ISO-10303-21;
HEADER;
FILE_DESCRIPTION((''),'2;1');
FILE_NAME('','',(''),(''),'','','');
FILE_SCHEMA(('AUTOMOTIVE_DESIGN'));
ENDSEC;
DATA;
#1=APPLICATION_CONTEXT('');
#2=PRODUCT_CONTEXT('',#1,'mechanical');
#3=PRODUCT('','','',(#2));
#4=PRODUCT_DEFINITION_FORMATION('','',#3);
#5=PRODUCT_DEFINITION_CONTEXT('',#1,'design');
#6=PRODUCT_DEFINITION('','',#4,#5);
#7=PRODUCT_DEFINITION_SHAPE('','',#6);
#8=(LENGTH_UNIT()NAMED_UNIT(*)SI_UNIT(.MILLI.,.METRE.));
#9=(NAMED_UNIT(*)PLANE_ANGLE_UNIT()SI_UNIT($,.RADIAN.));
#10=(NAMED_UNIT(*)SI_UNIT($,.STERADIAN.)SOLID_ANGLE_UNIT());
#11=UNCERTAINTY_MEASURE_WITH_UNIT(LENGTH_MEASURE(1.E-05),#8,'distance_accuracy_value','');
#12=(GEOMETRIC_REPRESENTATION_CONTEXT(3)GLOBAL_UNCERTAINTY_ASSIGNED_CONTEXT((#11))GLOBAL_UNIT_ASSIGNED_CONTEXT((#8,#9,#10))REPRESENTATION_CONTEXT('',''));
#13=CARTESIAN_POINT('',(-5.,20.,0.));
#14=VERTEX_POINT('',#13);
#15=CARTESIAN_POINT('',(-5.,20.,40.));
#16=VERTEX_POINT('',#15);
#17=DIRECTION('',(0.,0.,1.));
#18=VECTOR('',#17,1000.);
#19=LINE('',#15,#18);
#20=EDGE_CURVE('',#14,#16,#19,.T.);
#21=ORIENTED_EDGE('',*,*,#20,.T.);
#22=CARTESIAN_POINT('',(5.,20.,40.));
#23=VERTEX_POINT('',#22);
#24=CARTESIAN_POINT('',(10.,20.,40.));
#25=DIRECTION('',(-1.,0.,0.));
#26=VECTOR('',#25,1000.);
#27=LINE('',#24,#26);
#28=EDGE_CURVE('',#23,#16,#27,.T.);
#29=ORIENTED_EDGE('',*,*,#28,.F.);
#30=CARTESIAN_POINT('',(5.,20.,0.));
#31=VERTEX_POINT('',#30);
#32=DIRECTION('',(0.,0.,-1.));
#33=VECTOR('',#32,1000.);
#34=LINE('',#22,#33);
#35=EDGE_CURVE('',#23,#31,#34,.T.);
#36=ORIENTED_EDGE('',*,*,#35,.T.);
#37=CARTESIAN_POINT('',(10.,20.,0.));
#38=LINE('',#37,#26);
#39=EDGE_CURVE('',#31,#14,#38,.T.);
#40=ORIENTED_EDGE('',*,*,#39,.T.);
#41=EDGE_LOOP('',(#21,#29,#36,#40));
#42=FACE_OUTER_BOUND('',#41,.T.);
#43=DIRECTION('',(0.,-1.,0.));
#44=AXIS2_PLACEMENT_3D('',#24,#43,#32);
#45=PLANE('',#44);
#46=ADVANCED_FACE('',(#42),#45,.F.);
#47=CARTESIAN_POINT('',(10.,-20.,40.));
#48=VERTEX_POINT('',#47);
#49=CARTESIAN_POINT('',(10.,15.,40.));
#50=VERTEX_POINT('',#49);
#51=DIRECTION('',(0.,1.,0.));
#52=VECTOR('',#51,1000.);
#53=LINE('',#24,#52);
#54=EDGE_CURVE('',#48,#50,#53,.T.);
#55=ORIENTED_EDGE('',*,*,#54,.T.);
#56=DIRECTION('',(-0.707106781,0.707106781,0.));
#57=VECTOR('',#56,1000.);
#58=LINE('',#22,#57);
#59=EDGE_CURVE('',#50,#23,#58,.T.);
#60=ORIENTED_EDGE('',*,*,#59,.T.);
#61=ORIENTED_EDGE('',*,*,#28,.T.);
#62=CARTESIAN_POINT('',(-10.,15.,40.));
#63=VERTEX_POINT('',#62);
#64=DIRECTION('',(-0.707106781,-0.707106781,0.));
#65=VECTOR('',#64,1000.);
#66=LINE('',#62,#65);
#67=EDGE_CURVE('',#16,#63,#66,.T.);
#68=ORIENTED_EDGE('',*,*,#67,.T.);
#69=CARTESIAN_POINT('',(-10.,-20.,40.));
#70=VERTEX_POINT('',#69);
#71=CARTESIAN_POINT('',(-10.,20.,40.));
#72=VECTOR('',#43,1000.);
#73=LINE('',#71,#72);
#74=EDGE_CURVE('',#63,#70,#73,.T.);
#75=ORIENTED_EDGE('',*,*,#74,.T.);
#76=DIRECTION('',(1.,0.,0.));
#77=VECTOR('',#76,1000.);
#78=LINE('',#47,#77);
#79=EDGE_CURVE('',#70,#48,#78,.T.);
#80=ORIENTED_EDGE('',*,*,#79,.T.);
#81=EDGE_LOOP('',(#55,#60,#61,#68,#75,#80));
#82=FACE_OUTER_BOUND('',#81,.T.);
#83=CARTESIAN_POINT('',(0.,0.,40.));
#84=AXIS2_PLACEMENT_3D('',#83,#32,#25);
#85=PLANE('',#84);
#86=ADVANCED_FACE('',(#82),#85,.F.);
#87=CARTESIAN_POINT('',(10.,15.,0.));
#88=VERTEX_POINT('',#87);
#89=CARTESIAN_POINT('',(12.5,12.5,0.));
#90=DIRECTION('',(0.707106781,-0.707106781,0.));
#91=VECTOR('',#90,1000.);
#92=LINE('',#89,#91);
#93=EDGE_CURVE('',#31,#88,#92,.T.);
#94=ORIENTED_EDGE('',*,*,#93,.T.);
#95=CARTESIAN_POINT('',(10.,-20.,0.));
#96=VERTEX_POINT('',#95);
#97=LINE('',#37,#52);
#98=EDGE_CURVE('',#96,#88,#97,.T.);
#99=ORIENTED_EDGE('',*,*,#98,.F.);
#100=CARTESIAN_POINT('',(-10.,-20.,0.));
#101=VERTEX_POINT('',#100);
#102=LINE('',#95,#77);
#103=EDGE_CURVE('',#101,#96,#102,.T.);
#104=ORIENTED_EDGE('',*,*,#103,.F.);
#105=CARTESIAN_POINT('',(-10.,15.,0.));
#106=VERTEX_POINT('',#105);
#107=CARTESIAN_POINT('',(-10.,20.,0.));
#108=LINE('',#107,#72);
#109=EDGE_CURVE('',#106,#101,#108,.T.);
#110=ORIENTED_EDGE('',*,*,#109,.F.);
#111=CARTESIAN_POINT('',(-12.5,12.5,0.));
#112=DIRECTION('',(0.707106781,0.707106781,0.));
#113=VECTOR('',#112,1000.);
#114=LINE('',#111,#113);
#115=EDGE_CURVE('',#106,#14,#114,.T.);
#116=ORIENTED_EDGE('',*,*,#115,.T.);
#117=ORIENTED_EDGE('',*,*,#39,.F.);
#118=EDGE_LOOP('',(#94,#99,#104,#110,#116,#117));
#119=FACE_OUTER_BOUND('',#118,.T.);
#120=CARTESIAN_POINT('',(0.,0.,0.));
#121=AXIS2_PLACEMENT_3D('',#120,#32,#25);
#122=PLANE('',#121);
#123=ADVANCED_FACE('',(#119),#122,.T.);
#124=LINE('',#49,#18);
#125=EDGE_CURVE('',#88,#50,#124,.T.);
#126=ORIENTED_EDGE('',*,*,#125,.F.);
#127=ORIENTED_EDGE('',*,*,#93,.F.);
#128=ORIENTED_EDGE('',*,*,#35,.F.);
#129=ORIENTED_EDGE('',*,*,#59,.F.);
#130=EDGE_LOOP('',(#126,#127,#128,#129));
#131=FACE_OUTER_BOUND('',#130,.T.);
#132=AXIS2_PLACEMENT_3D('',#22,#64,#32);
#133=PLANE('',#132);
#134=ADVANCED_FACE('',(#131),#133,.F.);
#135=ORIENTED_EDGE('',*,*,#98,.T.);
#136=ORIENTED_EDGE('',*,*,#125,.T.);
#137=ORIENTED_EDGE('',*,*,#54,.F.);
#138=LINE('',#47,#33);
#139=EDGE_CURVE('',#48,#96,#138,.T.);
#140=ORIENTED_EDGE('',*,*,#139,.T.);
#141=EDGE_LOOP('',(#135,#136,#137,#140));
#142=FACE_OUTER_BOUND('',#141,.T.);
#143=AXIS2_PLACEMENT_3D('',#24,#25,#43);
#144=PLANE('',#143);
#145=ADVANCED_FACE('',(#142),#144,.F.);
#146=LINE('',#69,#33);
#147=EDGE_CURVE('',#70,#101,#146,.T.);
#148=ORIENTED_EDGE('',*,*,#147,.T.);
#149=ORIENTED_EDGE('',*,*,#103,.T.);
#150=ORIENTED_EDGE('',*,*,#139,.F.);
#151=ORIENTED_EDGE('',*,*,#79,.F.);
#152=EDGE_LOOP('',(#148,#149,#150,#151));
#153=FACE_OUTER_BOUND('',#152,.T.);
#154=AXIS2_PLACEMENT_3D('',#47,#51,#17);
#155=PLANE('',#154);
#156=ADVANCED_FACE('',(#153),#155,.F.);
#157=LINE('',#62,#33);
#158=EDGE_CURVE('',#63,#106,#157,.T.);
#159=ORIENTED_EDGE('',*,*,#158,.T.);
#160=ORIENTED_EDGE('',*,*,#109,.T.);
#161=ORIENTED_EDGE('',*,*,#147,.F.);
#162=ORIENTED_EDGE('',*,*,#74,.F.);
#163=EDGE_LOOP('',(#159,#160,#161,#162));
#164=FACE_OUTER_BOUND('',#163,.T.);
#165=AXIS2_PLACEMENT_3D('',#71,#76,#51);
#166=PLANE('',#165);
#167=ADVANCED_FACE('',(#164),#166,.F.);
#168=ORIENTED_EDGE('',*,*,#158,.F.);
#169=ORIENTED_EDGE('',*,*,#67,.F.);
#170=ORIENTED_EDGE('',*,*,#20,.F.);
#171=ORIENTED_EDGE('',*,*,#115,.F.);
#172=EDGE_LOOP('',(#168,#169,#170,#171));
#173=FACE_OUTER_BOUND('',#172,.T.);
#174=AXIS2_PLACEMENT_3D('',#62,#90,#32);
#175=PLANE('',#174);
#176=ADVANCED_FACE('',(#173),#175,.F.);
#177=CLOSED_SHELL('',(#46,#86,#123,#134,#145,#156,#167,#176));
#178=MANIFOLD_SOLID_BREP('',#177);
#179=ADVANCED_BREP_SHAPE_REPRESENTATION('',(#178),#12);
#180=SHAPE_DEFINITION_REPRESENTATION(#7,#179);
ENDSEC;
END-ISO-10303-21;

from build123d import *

# Parameters (mm, degrees)
SKETCH1_W           = 20
SKETCH1_H           = 40
BOSS_EXTRUDE1_DEPTH = 40
CHAMFER1_SIZE       = 5


with BuildPart() as part:
    # Sketch1 → Boss-Extrude1 (new body)
    with BuildSketch(Plane.XY):
        Rectangle(SKETCH1_W, SKETCH1_H)
    extrude(amount=BOSS_EXTRUDE1_DEPTH)

    # Chamfer1
    chamfer1_edges = [part.edges().sort_by_distance(p)[0] for p in [
        (-10, 20, 20),
        (10, 20, 20),
    ]]
    chamfer(chamfer1_edges, length=CHAMFER1_SIZE)


solid = part.part
